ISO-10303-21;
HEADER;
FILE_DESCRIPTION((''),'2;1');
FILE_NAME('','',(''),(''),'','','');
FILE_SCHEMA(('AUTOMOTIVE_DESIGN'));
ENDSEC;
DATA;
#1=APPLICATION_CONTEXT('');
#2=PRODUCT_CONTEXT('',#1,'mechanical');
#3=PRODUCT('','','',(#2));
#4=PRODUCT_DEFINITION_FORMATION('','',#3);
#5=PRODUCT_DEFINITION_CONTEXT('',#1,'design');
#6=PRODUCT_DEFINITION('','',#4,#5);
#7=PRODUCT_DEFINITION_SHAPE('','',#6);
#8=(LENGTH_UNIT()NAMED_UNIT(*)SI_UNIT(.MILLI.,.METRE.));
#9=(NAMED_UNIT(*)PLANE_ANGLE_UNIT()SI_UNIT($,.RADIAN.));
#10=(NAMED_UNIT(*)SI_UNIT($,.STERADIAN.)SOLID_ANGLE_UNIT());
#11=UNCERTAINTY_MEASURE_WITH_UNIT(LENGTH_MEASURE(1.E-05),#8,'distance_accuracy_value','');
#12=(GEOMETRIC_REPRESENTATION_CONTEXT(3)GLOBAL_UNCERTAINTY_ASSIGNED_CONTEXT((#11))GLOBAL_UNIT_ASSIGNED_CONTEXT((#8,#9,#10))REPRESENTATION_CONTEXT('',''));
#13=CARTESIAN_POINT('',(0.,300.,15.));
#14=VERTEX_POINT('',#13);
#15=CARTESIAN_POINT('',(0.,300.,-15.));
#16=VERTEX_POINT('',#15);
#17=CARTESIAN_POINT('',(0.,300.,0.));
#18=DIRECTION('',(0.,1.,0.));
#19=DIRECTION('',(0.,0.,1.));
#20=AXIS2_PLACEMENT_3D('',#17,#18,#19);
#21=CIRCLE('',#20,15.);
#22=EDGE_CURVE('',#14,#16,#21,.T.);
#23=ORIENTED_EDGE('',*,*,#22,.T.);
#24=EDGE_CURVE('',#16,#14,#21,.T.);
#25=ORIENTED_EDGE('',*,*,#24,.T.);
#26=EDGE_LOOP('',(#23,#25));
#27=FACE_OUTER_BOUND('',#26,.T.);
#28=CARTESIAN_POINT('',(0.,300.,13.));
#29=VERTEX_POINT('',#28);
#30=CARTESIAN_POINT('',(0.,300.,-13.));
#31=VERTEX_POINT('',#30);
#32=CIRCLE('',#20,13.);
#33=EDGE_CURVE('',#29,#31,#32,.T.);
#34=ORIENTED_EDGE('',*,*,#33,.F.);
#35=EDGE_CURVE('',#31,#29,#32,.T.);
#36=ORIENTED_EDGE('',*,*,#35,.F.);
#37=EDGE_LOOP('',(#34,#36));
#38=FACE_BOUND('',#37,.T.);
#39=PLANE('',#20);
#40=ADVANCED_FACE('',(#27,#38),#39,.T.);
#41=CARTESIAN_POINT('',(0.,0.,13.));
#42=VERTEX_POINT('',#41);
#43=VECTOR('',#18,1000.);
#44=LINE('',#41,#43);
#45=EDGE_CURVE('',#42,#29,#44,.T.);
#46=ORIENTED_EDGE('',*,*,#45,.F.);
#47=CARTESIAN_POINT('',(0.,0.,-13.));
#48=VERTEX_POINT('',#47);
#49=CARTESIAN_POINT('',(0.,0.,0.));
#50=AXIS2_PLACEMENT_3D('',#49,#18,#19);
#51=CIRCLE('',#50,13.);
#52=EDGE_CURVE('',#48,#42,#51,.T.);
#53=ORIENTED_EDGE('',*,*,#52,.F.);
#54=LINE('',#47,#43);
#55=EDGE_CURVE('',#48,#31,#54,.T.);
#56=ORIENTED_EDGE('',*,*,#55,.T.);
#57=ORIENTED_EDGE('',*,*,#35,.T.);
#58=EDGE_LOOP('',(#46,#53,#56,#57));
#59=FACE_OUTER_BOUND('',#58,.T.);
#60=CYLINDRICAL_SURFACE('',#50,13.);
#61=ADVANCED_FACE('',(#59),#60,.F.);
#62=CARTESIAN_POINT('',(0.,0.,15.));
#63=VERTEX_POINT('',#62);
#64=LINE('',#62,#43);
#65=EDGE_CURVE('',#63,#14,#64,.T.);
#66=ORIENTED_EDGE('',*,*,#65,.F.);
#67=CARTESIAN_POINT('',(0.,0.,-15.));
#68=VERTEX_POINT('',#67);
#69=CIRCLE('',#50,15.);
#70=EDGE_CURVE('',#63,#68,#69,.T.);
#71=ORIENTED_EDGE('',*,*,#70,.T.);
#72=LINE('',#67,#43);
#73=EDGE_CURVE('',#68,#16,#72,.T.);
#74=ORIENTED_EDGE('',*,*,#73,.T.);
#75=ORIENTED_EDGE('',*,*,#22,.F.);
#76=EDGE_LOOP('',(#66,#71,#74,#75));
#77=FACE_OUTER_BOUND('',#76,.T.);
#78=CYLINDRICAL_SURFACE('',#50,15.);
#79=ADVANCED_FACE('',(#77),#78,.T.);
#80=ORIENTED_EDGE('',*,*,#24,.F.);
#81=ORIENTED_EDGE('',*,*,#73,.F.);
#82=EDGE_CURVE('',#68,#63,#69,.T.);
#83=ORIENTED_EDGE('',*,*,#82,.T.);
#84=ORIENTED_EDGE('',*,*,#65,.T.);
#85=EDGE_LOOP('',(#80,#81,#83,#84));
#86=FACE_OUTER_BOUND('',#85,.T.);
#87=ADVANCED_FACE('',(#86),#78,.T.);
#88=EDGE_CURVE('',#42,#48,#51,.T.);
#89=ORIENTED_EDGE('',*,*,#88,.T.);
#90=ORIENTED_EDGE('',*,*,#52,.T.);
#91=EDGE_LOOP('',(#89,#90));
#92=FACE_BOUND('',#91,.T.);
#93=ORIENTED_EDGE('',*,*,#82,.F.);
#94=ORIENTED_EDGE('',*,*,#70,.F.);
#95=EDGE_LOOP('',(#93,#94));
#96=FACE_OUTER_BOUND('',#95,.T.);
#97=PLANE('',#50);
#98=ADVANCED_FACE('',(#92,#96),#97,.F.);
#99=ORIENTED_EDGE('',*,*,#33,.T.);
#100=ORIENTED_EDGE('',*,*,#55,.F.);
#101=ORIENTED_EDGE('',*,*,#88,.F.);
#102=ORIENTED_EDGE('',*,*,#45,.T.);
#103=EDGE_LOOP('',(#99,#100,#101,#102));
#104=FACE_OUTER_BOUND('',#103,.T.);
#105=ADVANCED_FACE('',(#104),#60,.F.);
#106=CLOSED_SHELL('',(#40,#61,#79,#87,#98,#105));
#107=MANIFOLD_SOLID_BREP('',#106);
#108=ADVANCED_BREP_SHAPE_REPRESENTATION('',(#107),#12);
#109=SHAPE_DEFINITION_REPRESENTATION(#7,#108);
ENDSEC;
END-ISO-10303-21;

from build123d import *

# Parameters (mm, degrees)
SWEEP_THIN1_PROFILE_R   = 15
SWEEP_THIN1_PROFILE_R_2 = 13


with BuildPart() as part:
    # Sweep-Thin1: sweep along a path in Sketch1
    with BuildLine(Plane.XY) as sweep_thin1_path:
        Line((0, 0), (0, 300))
    # Sweep-Thin1 profile (on start of the path) → Sweep-Thin1 (sweep)
    with BuildSketch(Plane.ZX):
        Circle(SWEEP_THIN1_PROFILE_R)
        Circle(SWEEP_THIN1_PROFILE_R_2, mode=Mode.SUBTRACT)
    sweep(path=sweep_thin1_path.line)


solid = part.part
